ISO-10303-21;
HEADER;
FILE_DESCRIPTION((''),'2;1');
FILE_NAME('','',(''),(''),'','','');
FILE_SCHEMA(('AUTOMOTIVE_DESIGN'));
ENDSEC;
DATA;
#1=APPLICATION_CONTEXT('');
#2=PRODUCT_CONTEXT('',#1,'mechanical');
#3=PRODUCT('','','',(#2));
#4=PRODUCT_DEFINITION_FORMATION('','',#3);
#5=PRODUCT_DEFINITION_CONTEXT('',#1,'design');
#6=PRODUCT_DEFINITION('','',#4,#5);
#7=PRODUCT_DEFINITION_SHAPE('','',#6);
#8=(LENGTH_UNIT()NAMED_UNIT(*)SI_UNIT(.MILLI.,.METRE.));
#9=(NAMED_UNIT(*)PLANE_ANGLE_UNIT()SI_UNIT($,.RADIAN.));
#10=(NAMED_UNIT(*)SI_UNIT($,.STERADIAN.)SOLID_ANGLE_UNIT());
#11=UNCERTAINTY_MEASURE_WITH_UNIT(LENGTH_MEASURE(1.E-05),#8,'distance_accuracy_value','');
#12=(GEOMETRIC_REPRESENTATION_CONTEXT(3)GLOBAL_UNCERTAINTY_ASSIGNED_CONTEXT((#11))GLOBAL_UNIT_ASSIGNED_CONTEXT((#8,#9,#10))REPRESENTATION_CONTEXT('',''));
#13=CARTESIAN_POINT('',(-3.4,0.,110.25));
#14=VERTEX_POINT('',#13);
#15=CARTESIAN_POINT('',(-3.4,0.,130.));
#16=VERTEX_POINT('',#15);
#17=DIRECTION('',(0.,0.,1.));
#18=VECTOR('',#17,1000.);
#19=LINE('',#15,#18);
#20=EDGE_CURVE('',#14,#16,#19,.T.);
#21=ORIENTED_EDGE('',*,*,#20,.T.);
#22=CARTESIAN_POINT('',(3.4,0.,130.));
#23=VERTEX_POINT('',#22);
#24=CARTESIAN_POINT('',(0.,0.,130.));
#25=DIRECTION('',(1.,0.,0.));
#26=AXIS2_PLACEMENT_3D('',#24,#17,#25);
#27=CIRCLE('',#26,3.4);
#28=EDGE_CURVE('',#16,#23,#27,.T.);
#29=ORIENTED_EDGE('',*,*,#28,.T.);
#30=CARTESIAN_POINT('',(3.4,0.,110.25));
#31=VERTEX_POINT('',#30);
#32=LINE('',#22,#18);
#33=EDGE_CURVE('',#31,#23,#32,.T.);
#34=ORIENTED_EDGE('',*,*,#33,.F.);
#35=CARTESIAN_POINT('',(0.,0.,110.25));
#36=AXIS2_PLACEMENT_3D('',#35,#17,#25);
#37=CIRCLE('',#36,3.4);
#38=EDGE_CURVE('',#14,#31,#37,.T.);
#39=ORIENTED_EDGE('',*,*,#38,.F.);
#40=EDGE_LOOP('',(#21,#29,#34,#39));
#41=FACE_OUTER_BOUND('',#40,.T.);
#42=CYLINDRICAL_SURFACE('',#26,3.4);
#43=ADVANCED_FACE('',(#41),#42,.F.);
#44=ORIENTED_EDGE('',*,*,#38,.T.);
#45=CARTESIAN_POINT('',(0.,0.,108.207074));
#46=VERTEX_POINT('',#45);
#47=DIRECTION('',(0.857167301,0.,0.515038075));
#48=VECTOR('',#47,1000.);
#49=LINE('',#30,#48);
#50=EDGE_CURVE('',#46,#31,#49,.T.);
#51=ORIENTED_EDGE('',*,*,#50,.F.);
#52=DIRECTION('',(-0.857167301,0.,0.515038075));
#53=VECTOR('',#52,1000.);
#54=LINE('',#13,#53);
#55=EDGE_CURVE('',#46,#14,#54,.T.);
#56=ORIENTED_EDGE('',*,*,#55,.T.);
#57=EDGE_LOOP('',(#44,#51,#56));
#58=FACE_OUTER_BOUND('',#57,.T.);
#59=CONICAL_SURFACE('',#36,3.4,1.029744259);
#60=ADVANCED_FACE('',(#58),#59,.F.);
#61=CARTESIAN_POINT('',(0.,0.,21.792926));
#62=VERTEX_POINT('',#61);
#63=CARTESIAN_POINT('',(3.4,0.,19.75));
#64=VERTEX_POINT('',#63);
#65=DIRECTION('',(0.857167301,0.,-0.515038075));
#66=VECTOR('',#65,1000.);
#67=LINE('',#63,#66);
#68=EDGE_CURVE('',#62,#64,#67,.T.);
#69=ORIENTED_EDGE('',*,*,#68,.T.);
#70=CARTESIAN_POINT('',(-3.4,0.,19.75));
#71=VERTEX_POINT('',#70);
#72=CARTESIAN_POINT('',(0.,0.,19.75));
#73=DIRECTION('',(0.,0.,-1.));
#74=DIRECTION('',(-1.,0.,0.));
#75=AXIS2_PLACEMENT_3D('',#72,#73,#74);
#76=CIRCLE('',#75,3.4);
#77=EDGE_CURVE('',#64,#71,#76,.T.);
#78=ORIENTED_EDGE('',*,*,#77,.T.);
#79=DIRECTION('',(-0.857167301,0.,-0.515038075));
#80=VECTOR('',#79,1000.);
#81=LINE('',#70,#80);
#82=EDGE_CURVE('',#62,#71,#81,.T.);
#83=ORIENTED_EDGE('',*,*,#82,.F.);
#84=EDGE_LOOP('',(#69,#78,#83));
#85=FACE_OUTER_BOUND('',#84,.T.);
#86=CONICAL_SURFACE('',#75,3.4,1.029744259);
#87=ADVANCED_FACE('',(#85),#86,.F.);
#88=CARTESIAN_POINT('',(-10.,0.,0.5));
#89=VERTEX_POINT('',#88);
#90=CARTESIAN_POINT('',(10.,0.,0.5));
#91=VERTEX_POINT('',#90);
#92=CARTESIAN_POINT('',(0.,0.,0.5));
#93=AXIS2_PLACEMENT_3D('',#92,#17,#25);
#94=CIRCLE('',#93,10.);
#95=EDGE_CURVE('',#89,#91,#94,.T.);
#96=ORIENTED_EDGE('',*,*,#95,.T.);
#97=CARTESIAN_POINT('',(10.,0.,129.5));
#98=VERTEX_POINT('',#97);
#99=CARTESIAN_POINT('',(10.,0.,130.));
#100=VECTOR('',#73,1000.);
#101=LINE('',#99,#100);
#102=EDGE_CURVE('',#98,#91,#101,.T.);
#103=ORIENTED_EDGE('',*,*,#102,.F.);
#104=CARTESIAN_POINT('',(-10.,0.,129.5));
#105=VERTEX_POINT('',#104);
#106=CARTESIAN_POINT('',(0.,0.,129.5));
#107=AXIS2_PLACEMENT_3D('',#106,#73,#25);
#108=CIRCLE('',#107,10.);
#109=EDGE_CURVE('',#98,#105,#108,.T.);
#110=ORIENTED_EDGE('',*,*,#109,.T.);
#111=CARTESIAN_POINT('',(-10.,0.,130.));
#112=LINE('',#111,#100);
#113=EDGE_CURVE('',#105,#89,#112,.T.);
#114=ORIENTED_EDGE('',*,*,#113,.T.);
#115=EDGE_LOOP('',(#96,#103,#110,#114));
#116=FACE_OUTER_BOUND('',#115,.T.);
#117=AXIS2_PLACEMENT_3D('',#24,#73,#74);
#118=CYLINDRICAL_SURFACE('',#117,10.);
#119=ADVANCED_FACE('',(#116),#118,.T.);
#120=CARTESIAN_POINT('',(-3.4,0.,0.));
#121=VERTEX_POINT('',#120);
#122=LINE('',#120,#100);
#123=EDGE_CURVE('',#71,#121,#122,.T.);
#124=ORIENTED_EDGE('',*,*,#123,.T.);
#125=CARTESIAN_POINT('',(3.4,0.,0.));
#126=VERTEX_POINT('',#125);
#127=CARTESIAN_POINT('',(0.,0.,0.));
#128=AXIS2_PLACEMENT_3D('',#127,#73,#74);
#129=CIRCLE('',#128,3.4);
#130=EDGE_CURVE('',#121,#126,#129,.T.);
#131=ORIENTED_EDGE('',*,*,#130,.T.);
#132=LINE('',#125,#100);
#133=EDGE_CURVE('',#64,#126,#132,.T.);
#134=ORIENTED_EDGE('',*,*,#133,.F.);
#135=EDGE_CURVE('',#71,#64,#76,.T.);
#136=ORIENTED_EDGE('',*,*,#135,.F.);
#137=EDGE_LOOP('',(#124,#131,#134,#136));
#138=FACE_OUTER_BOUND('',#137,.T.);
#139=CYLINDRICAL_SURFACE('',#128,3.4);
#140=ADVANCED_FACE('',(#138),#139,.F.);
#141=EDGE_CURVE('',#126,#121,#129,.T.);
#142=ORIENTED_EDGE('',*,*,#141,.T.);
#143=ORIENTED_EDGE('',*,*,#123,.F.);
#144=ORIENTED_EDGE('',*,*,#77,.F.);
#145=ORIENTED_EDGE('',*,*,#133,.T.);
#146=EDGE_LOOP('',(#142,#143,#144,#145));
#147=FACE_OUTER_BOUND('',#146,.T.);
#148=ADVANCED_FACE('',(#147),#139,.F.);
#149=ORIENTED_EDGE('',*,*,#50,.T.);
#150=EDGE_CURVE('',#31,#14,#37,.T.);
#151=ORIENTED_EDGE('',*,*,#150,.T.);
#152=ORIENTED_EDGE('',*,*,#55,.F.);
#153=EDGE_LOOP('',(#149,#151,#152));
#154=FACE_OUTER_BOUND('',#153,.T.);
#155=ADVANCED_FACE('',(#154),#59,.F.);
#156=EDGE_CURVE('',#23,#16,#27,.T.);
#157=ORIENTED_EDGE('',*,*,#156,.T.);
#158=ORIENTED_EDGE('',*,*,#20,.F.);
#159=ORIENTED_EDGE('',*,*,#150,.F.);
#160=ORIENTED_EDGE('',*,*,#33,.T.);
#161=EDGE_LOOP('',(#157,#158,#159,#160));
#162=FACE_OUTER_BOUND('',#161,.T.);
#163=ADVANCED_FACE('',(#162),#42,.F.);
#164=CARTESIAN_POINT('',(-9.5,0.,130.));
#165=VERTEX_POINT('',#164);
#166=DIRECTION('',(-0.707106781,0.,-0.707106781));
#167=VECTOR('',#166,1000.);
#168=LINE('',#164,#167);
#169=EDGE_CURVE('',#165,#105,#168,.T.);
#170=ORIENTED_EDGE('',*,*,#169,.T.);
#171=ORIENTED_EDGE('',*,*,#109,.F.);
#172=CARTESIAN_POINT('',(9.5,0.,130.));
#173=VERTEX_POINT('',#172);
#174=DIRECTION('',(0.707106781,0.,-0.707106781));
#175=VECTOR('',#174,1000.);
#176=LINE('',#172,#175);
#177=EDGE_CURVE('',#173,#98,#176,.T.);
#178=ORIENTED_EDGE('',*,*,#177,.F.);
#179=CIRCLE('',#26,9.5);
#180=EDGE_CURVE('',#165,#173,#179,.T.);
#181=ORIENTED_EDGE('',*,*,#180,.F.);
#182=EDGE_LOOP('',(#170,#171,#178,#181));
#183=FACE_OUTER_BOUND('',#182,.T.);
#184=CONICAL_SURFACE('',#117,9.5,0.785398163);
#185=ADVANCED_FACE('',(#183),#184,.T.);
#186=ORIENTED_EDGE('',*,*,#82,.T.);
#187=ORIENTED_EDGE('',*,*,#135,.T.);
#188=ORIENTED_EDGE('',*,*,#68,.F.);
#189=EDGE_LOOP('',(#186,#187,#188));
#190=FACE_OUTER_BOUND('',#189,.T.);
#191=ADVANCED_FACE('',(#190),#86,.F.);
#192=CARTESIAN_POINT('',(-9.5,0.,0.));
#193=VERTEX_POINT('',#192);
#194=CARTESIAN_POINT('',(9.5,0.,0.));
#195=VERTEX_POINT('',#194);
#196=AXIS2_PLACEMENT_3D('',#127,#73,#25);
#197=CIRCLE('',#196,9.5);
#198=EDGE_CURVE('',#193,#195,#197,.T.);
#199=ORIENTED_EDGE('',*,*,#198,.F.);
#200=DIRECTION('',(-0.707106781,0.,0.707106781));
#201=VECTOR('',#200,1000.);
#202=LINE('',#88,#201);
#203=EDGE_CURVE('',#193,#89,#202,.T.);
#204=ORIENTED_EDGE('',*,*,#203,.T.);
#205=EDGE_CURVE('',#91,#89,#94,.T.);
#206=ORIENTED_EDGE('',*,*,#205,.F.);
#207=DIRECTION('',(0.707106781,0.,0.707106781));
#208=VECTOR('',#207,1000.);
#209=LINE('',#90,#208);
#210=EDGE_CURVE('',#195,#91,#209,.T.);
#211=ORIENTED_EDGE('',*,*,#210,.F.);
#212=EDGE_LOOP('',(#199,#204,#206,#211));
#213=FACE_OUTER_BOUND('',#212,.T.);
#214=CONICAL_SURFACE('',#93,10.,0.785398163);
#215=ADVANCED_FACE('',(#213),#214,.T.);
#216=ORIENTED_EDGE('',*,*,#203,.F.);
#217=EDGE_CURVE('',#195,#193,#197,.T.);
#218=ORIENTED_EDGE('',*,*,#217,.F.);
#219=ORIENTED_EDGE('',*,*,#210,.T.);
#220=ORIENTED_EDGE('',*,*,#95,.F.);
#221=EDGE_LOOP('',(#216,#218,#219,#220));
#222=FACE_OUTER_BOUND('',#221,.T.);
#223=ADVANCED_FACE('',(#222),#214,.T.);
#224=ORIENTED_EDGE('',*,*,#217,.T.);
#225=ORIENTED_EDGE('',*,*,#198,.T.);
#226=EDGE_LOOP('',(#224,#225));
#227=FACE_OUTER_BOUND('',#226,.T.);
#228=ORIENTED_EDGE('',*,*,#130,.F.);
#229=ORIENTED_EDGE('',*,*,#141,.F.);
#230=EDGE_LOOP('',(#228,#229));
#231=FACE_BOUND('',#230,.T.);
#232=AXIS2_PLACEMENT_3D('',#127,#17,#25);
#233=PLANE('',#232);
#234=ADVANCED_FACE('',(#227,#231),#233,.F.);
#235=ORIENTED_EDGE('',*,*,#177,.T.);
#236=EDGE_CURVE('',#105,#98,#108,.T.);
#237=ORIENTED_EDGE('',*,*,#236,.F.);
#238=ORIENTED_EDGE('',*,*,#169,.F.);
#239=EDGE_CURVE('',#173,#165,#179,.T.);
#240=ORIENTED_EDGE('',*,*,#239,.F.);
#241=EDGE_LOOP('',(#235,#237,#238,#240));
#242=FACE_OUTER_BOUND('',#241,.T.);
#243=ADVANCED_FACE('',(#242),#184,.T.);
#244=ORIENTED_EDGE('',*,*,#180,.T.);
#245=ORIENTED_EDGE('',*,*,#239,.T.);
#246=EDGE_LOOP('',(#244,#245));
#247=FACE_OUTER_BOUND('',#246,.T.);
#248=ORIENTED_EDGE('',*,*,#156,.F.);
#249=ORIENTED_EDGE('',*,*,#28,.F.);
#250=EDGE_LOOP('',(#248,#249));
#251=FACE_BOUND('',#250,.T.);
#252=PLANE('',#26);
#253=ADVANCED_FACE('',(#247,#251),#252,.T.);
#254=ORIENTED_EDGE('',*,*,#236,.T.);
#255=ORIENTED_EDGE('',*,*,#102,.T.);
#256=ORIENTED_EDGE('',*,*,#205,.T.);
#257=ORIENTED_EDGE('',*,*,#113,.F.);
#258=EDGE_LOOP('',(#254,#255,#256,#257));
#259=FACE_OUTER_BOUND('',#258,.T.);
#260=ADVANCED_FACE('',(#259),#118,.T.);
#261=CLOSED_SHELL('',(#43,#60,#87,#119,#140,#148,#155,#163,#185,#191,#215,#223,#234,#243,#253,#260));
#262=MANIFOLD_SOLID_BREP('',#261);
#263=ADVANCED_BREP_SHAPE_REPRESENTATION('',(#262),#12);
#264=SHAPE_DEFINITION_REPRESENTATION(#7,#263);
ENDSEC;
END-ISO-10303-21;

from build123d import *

# Parameters (mm, degrees)
SKETCH_1_R             = 10
EXTRUDE_1_DEPTH        = 130
HOLE_WIZARD_M8_1_D     = 6.8
HOLE_WIZARD_M8_1_DEPTH = 19.75
HOLE_WIZARD_M8_1_TIP   = 2.042926105
HOLE_WIZARD_M8_2_D     = 6.8
HOLE_WIZARD_M8_2_DEPTH = 19.75
HOLE_WIZARD_M8_2_TIP   = 2.042926105
CHAMFER_1_SIZE         = 0.5


with BuildPart() as part:
    # 草图1 → 凸台-拉伸1 (new body)
    with BuildSketch(Plane.XY):
        Circle(SKETCH_1_R)
    extrude(amount=EXTRUDE_1_DEPTH)

    # M8 螺纹孔1
    with Locations(Plane(origin=(0, 0, 0), x_dir=(-1, 0, 0), z_dir=(0, 0, -1))):
        with Locations((0, 0)):
            Hole(HOLE_WIZARD_M8_1_D / 2, depth=HOLE_WIZARD_M8_1_DEPTH)
            with Locations((0, 0, -(HOLE_WIZARD_M8_1_DEPTH + HOLE_WIZARD_M8_1_TIP / 2))):  # 118° drill point
                Cone(0, HOLE_WIZARD_M8_1_D / 2, HOLE_WIZARD_M8_1_TIP, mode=Mode.SUBTRACT)

    # M8 螺纹孔2
    with Locations(Plane.XY.offset(130)):
        with Locations((0, 0)):
            Hole(HOLE_WIZARD_M8_2_D / 2, depth=HOLE_WIZARD_M8_2_DEPTH)
            with Locations((0, 0, -(HOLE_WIZARD_M8_2_DEPTH + HOLE_WIZARD_M8_2_TIP / 2))):  # 118° drill point
                Cone(0, HOLE_WIZARD_M8_2_D / 2, HOLE_WIZARD_M8_2_TIP, mode=Mode.SUBTRACT)

    # 倒角1
    chamfer_1_edges = [part.edges().sort_by_distance(p)[0] for p in [
        (-10, 0, 0),
        (-10, 0, 130),
    ]]
    chamfer(chamfer_1_edges, length=CHAMFER_1_SIZE)


solid = part.part
